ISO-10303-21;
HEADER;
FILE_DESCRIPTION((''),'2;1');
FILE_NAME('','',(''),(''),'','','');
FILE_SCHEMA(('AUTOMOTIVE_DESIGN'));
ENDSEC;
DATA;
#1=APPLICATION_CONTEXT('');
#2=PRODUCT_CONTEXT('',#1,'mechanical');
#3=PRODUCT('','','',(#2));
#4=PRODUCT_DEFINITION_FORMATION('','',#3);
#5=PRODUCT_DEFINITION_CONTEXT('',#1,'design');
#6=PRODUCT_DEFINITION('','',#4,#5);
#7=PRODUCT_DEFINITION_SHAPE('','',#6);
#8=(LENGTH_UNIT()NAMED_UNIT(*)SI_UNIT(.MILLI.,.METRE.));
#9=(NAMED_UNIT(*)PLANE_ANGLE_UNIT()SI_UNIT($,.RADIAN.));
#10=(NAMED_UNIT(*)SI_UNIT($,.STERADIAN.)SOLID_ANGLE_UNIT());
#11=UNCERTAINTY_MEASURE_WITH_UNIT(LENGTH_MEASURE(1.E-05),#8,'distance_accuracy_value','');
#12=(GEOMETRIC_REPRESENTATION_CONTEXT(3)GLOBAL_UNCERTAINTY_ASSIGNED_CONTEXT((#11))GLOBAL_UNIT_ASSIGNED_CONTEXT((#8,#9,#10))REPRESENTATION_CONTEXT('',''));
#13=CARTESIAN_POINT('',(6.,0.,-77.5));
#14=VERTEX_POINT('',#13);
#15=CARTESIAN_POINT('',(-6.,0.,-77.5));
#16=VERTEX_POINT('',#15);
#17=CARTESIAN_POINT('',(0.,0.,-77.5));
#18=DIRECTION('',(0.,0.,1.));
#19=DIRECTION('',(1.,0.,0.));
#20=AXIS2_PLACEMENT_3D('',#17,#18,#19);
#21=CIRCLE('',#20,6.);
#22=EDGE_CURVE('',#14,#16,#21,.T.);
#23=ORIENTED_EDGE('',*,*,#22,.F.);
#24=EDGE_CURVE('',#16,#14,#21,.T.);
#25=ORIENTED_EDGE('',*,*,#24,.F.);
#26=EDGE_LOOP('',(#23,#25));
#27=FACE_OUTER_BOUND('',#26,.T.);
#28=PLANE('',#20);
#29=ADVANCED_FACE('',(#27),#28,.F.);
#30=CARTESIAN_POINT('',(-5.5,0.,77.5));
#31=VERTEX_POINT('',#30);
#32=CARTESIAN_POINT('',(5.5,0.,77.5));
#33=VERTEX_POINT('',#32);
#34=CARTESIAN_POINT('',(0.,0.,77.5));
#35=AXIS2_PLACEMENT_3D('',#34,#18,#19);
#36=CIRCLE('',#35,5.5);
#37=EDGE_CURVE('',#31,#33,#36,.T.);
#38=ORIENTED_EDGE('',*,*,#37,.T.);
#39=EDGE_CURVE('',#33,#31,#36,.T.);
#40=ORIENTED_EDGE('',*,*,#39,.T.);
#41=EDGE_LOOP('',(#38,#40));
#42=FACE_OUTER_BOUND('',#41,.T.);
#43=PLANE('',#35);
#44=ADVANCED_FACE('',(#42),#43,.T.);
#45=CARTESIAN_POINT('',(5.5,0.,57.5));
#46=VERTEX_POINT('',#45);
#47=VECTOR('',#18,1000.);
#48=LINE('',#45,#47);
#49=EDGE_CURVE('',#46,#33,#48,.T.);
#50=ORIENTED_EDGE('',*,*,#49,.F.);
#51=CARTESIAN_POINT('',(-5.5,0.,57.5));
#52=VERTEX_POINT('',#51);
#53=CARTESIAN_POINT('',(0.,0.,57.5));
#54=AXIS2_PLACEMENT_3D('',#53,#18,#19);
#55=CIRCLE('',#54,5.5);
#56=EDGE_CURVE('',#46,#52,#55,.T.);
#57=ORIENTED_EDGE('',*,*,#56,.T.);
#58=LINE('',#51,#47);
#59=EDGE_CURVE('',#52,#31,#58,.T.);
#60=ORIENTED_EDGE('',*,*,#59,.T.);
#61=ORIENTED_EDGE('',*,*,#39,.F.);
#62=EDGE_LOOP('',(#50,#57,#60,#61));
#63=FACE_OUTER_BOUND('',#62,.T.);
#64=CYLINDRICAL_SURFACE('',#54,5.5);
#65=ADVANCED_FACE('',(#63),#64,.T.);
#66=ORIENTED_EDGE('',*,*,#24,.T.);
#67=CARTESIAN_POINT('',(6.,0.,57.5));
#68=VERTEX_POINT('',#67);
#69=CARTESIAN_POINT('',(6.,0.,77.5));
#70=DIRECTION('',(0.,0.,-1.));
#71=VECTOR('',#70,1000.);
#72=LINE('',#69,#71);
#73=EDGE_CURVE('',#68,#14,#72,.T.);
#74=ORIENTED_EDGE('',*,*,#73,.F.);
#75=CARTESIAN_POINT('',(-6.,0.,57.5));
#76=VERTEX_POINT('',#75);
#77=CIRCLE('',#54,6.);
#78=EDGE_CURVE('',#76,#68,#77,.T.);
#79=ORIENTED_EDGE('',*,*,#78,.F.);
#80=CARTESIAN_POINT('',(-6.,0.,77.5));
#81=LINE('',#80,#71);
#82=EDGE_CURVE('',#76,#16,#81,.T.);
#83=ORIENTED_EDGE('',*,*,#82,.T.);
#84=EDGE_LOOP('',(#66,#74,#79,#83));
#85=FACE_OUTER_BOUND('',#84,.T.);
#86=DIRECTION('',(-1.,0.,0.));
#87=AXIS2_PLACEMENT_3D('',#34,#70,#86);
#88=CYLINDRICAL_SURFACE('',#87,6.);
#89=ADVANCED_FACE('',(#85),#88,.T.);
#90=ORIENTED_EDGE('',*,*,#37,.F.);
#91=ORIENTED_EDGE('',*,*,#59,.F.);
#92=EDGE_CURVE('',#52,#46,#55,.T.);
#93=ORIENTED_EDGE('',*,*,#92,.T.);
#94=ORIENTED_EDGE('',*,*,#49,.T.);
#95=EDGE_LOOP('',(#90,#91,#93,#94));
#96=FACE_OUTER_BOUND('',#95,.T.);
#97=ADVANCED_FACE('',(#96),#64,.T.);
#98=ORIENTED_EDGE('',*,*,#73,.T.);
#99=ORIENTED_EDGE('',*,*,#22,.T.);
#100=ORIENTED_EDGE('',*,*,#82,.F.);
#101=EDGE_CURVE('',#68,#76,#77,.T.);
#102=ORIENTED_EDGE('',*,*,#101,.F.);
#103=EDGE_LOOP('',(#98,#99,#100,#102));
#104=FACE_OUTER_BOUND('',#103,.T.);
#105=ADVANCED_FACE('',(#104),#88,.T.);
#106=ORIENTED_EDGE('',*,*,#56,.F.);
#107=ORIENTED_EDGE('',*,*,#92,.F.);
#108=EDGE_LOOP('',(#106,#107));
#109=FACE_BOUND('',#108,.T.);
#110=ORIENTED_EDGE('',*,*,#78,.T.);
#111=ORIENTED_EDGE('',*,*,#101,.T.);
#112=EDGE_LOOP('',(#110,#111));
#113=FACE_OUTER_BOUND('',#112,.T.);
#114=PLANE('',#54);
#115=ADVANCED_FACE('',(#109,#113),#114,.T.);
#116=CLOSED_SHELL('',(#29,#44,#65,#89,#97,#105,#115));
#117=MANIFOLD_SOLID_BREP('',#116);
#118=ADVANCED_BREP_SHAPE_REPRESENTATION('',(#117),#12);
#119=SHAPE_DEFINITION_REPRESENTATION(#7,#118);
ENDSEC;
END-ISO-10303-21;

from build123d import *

# Parameters (mm, degrees)
SKETCH_1_R          = 6
EXTRUDE_3_DEPTH     = 77.5
SKETCH_3_R          = 6
SKETCH_3_R_2        = 5.5
CUT_EXTRUDE_1_DEPTH = 20


with BuildPart() as part:
    # 草图1 → 凸台-拉伸3 (new, symmetric)
    with BuildSketch(Plane.XY):
        Circle(SKETCH_1_R)
    extrude(amount=EXTRUDE_3_DEPTH, both=True)

    # 草图3 → 切除-拉伸1 (cut)
    with BuildSketch(Plane.XY.offset(77.5)):
        Circle(SKETCH_3_R)
        Circle(SKETCH_3_R_2, mode=Mode.SUBTRACT)
    extrude(amount=-CUT_EXTRUDE_1_DEPTH, mode=Mode.SUBTRACT)


solid = part.part
